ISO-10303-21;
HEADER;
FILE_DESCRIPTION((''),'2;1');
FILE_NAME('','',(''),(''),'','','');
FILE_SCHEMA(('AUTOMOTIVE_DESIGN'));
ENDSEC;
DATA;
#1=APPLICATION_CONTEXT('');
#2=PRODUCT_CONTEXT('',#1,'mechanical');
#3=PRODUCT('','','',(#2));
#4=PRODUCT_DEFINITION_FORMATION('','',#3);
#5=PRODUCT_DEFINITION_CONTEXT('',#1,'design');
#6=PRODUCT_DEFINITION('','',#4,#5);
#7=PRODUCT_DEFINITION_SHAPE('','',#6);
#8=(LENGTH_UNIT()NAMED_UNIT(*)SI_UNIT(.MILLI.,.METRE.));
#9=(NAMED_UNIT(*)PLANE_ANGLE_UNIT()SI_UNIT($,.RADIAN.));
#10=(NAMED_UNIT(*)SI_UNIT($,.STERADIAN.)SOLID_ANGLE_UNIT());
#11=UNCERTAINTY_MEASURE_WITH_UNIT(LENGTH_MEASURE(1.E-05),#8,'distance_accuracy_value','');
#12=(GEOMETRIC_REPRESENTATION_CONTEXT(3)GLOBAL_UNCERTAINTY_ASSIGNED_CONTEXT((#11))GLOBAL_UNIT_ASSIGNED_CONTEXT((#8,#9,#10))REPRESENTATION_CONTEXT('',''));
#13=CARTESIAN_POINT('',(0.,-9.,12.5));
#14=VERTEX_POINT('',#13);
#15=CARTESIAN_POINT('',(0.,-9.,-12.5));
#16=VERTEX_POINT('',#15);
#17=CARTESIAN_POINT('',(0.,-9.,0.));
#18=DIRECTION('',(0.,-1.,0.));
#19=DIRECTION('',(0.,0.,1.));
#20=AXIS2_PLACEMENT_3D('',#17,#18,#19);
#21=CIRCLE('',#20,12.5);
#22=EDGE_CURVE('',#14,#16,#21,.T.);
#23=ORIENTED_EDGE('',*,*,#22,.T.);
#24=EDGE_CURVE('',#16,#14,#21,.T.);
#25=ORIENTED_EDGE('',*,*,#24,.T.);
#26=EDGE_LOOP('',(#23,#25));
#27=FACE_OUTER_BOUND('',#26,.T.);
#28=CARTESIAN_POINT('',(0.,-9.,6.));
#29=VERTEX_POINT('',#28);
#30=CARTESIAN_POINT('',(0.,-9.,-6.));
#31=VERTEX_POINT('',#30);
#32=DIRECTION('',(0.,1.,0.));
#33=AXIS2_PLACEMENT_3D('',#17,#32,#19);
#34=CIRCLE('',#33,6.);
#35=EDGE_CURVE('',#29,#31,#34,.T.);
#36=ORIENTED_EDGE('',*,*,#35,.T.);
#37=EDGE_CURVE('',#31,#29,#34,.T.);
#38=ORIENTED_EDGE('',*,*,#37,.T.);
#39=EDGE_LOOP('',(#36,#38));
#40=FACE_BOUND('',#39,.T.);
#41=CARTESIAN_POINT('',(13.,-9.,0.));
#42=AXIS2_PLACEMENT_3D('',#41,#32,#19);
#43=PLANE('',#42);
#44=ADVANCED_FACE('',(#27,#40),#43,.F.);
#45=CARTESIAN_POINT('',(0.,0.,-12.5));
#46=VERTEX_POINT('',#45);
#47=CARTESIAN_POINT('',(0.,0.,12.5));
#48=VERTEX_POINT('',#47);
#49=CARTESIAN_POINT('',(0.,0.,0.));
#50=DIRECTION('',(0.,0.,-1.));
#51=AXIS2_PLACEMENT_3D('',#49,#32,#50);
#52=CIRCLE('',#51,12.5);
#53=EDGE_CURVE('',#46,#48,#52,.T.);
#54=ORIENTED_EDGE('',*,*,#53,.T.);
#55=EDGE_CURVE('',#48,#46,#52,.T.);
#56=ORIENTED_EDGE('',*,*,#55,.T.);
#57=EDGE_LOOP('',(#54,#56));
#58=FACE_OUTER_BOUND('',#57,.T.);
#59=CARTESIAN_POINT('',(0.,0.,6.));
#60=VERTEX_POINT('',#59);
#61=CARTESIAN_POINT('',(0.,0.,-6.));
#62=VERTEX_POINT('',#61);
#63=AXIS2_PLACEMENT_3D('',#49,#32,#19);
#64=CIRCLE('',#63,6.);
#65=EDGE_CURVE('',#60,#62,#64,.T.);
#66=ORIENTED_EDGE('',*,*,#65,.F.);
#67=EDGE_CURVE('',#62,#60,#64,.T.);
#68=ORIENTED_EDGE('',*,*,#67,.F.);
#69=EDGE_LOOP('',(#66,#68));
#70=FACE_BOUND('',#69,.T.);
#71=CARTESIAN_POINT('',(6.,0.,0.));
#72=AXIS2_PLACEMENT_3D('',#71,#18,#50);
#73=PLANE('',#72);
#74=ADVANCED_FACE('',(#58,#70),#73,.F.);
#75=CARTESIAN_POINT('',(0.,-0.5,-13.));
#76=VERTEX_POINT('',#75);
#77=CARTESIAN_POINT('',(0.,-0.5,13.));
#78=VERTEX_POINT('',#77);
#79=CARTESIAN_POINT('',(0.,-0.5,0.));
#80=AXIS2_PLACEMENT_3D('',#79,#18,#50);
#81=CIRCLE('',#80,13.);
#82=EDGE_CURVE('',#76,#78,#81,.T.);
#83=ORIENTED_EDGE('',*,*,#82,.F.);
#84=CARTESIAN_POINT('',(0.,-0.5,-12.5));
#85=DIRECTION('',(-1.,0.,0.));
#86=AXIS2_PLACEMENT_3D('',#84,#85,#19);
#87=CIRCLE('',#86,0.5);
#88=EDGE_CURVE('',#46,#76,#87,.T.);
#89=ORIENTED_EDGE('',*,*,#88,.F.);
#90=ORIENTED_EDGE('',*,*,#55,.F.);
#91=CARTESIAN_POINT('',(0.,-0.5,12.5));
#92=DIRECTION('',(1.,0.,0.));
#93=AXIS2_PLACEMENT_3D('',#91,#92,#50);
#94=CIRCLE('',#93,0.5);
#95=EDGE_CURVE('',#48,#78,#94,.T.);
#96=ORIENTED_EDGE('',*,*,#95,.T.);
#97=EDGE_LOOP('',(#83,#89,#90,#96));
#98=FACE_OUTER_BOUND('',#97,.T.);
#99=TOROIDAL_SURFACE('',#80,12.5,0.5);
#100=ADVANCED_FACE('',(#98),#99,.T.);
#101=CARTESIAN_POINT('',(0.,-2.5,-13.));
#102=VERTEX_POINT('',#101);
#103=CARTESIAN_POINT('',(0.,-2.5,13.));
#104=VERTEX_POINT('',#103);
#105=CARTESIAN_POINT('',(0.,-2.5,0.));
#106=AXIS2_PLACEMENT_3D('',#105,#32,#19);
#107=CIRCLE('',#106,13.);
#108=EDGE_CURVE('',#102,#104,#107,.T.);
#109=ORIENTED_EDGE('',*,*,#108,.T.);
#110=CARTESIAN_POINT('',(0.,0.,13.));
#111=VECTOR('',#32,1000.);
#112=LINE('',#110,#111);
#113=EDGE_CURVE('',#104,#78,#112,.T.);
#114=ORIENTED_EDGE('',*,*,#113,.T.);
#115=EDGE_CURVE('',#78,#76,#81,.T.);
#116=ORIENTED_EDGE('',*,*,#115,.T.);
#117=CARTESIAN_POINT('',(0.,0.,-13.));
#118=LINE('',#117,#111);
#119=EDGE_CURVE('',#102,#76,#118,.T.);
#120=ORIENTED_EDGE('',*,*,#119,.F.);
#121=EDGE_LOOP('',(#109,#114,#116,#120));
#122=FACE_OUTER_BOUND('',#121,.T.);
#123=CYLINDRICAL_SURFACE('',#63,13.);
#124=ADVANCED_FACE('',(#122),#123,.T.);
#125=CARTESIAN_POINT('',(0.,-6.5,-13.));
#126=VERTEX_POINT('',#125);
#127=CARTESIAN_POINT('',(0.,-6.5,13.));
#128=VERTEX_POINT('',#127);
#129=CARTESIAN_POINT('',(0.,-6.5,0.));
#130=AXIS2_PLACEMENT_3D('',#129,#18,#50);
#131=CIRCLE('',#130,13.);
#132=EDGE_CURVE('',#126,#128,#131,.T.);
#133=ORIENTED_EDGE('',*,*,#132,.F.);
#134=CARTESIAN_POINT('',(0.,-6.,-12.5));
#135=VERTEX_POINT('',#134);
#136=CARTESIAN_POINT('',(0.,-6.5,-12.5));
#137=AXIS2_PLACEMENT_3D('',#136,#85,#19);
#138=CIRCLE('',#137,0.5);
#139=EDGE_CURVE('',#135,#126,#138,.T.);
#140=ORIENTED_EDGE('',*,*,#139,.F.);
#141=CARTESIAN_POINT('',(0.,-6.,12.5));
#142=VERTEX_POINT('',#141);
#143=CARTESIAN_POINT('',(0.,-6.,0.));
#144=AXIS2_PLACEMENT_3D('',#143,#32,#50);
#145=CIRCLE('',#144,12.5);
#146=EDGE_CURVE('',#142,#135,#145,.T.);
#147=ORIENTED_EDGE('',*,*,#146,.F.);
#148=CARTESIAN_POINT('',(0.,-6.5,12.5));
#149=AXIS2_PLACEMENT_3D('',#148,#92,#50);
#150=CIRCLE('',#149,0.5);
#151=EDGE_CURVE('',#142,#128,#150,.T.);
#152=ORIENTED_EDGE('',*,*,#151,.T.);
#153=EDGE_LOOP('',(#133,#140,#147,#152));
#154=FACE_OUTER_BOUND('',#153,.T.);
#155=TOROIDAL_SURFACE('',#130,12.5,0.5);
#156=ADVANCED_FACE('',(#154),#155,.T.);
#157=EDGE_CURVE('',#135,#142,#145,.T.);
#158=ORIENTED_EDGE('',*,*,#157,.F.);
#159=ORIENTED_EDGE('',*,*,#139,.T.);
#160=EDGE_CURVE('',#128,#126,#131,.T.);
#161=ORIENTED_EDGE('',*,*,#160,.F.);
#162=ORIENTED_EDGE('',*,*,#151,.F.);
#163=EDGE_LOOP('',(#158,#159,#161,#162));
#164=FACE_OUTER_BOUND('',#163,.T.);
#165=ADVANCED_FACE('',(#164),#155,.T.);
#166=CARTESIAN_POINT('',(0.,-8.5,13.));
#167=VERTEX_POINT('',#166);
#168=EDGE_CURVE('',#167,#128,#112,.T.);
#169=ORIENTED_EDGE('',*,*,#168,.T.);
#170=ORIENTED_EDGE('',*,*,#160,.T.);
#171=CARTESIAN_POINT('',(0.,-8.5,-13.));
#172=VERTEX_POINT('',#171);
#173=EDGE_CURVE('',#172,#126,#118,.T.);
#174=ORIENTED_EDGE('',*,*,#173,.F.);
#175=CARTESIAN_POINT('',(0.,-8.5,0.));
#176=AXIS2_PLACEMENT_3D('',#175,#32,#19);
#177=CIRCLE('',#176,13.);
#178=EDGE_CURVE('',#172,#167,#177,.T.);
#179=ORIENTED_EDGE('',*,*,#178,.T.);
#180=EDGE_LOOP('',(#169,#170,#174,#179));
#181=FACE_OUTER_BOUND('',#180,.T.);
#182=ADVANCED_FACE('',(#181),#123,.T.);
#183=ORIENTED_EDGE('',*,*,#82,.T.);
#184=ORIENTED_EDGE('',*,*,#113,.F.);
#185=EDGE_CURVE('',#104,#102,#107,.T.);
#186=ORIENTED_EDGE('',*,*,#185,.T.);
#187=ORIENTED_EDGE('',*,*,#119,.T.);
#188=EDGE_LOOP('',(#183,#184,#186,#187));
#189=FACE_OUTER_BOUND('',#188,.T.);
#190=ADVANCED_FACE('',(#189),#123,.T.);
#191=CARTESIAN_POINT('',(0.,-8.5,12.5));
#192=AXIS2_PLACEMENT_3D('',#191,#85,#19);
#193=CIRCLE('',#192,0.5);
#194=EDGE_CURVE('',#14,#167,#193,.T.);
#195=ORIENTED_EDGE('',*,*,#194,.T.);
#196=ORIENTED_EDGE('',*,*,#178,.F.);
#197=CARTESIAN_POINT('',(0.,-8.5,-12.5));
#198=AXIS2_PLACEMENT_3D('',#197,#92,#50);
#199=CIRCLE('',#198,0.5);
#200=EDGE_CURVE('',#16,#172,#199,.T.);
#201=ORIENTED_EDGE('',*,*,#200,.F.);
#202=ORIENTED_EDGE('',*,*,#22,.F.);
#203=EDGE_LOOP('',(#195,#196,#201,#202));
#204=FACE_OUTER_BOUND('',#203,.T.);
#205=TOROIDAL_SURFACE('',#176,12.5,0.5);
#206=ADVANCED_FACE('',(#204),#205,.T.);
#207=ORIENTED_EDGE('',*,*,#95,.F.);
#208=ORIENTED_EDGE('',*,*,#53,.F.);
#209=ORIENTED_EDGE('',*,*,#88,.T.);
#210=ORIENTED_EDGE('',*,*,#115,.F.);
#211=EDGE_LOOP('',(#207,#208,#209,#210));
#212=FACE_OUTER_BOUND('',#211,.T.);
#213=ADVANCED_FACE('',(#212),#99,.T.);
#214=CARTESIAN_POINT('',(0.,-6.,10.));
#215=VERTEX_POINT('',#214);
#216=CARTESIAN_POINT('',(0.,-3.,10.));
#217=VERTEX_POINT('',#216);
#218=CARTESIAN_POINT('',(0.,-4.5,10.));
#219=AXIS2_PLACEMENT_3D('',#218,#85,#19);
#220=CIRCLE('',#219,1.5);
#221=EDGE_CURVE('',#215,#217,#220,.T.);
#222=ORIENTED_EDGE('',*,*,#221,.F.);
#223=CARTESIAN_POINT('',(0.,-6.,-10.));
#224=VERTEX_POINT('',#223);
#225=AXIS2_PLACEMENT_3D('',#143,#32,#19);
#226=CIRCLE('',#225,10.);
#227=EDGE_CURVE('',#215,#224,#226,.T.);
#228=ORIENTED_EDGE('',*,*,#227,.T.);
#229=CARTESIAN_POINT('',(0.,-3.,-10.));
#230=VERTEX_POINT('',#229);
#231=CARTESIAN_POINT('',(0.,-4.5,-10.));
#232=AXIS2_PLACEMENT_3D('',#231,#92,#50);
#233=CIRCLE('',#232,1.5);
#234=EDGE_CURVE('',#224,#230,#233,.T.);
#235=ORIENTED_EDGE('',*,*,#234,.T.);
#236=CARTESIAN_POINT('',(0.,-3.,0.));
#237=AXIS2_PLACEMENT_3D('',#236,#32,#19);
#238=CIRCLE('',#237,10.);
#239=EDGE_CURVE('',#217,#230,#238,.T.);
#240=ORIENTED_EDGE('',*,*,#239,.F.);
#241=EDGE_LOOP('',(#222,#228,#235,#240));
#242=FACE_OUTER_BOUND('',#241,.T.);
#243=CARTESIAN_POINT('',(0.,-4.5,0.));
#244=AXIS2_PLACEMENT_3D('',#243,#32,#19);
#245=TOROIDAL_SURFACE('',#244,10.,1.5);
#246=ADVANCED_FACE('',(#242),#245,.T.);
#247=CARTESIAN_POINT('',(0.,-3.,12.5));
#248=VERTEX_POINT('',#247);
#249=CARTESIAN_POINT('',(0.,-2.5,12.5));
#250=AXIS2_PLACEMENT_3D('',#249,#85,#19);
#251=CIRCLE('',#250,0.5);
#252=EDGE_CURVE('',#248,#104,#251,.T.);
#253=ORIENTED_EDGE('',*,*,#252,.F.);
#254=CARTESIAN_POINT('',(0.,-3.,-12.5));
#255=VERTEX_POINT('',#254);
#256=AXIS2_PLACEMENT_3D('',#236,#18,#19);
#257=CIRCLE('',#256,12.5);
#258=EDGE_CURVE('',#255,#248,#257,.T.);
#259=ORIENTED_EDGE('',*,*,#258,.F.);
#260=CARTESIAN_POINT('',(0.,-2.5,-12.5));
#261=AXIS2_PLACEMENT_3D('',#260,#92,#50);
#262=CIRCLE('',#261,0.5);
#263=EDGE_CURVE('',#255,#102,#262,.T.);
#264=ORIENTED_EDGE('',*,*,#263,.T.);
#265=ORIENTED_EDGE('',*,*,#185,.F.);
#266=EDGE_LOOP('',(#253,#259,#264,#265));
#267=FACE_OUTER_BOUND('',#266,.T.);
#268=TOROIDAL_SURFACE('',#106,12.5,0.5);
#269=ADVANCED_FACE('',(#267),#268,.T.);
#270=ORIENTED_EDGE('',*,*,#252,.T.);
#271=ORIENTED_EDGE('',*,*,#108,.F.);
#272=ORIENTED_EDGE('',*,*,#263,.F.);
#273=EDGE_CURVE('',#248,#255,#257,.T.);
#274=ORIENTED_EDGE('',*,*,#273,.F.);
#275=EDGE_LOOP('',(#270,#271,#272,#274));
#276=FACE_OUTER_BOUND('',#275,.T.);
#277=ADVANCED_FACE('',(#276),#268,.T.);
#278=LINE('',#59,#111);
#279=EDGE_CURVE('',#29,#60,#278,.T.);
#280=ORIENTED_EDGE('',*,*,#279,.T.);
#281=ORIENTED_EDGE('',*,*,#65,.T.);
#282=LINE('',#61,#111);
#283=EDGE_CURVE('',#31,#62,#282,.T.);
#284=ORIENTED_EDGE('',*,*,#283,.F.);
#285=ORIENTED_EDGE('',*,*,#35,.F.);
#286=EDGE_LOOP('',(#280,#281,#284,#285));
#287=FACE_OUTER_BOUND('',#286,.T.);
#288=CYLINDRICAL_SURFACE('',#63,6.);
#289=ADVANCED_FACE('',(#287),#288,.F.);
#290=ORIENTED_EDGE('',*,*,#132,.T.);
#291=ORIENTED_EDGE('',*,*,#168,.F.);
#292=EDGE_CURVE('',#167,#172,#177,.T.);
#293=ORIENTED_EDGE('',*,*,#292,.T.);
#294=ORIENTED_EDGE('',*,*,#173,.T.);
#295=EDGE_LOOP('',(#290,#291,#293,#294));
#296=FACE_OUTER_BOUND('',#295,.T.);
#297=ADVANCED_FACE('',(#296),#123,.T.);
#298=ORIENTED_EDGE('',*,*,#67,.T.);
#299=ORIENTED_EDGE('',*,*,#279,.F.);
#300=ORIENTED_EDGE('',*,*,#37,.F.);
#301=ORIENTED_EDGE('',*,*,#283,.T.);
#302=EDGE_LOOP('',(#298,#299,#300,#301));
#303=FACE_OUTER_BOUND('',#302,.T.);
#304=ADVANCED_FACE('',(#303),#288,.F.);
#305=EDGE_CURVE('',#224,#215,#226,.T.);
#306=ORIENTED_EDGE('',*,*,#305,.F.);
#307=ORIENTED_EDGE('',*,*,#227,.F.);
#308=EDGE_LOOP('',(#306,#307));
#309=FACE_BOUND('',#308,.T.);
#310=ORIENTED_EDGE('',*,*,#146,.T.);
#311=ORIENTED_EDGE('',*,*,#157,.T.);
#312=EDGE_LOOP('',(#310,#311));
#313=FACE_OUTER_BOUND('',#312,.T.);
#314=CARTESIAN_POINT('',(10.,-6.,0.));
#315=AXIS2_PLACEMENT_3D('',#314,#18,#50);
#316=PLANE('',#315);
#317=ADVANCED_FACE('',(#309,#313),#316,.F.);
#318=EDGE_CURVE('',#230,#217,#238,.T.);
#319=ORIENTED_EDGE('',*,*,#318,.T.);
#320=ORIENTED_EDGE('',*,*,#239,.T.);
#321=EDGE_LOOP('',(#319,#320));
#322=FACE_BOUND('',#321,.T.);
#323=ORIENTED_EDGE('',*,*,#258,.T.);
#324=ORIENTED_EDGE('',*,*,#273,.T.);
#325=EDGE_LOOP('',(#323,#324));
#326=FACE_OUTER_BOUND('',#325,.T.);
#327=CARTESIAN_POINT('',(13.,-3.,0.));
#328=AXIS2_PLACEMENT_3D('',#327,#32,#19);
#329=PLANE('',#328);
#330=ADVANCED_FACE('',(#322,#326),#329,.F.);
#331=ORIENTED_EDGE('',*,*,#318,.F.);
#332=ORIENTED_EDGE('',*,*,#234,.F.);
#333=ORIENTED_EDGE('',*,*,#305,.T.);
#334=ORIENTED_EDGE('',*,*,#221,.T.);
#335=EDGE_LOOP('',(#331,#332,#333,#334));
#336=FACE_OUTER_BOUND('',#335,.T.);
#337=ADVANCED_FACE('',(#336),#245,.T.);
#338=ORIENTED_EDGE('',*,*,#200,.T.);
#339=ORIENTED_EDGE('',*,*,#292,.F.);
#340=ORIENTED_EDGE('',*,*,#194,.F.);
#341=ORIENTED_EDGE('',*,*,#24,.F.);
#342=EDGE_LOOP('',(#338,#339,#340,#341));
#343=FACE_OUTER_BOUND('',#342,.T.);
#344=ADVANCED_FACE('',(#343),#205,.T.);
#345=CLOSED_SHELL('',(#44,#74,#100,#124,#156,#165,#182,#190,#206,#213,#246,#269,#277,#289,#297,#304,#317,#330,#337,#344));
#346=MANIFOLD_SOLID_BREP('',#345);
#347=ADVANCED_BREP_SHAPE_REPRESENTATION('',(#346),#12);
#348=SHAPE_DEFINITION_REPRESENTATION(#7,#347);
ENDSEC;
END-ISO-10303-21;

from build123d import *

# Parameters (mm, degrees)
FILLET1_R = 0.5


with BuildPart() as part:
    # Sketch1 → Revolve1 (revolve)
    with BuildSketch(Plane.XY, mode=Mode.PRIVATE) as revolve1_sk:
        with BuildLine():
            Line((6, 0), (13, 0))
            Line((13, 0), (13, -3))
            Line((13, -3), (10, -3))
            ThreePointArc((10, -3), (11.5, -4.5), (10, -6))
            Line((10, -6), (13, -6))
            Line((13, -6), (13, -9))
            Line((13, -9), (6, -9))
            Line((6, -9), (6, 0))
        make_face()
    revolve(revolve1_sk.sketch.rotate(Axis((0, 0, 0), (0, -1, 0)), 90), axis=Axis((0, 0, 0), (0, -1, 0)))

    # Fillet1
    fillet1_edges = [part.edges().sort_by_distance(p)[0] for p in [
        (0, 0, -13),
        (0, -9, -13),
        (0, -6, -13),
        (0, -3, -13),
    ]]
    fillet(fillet1_edges, radius=FILLET1_R)


solid = part.part
